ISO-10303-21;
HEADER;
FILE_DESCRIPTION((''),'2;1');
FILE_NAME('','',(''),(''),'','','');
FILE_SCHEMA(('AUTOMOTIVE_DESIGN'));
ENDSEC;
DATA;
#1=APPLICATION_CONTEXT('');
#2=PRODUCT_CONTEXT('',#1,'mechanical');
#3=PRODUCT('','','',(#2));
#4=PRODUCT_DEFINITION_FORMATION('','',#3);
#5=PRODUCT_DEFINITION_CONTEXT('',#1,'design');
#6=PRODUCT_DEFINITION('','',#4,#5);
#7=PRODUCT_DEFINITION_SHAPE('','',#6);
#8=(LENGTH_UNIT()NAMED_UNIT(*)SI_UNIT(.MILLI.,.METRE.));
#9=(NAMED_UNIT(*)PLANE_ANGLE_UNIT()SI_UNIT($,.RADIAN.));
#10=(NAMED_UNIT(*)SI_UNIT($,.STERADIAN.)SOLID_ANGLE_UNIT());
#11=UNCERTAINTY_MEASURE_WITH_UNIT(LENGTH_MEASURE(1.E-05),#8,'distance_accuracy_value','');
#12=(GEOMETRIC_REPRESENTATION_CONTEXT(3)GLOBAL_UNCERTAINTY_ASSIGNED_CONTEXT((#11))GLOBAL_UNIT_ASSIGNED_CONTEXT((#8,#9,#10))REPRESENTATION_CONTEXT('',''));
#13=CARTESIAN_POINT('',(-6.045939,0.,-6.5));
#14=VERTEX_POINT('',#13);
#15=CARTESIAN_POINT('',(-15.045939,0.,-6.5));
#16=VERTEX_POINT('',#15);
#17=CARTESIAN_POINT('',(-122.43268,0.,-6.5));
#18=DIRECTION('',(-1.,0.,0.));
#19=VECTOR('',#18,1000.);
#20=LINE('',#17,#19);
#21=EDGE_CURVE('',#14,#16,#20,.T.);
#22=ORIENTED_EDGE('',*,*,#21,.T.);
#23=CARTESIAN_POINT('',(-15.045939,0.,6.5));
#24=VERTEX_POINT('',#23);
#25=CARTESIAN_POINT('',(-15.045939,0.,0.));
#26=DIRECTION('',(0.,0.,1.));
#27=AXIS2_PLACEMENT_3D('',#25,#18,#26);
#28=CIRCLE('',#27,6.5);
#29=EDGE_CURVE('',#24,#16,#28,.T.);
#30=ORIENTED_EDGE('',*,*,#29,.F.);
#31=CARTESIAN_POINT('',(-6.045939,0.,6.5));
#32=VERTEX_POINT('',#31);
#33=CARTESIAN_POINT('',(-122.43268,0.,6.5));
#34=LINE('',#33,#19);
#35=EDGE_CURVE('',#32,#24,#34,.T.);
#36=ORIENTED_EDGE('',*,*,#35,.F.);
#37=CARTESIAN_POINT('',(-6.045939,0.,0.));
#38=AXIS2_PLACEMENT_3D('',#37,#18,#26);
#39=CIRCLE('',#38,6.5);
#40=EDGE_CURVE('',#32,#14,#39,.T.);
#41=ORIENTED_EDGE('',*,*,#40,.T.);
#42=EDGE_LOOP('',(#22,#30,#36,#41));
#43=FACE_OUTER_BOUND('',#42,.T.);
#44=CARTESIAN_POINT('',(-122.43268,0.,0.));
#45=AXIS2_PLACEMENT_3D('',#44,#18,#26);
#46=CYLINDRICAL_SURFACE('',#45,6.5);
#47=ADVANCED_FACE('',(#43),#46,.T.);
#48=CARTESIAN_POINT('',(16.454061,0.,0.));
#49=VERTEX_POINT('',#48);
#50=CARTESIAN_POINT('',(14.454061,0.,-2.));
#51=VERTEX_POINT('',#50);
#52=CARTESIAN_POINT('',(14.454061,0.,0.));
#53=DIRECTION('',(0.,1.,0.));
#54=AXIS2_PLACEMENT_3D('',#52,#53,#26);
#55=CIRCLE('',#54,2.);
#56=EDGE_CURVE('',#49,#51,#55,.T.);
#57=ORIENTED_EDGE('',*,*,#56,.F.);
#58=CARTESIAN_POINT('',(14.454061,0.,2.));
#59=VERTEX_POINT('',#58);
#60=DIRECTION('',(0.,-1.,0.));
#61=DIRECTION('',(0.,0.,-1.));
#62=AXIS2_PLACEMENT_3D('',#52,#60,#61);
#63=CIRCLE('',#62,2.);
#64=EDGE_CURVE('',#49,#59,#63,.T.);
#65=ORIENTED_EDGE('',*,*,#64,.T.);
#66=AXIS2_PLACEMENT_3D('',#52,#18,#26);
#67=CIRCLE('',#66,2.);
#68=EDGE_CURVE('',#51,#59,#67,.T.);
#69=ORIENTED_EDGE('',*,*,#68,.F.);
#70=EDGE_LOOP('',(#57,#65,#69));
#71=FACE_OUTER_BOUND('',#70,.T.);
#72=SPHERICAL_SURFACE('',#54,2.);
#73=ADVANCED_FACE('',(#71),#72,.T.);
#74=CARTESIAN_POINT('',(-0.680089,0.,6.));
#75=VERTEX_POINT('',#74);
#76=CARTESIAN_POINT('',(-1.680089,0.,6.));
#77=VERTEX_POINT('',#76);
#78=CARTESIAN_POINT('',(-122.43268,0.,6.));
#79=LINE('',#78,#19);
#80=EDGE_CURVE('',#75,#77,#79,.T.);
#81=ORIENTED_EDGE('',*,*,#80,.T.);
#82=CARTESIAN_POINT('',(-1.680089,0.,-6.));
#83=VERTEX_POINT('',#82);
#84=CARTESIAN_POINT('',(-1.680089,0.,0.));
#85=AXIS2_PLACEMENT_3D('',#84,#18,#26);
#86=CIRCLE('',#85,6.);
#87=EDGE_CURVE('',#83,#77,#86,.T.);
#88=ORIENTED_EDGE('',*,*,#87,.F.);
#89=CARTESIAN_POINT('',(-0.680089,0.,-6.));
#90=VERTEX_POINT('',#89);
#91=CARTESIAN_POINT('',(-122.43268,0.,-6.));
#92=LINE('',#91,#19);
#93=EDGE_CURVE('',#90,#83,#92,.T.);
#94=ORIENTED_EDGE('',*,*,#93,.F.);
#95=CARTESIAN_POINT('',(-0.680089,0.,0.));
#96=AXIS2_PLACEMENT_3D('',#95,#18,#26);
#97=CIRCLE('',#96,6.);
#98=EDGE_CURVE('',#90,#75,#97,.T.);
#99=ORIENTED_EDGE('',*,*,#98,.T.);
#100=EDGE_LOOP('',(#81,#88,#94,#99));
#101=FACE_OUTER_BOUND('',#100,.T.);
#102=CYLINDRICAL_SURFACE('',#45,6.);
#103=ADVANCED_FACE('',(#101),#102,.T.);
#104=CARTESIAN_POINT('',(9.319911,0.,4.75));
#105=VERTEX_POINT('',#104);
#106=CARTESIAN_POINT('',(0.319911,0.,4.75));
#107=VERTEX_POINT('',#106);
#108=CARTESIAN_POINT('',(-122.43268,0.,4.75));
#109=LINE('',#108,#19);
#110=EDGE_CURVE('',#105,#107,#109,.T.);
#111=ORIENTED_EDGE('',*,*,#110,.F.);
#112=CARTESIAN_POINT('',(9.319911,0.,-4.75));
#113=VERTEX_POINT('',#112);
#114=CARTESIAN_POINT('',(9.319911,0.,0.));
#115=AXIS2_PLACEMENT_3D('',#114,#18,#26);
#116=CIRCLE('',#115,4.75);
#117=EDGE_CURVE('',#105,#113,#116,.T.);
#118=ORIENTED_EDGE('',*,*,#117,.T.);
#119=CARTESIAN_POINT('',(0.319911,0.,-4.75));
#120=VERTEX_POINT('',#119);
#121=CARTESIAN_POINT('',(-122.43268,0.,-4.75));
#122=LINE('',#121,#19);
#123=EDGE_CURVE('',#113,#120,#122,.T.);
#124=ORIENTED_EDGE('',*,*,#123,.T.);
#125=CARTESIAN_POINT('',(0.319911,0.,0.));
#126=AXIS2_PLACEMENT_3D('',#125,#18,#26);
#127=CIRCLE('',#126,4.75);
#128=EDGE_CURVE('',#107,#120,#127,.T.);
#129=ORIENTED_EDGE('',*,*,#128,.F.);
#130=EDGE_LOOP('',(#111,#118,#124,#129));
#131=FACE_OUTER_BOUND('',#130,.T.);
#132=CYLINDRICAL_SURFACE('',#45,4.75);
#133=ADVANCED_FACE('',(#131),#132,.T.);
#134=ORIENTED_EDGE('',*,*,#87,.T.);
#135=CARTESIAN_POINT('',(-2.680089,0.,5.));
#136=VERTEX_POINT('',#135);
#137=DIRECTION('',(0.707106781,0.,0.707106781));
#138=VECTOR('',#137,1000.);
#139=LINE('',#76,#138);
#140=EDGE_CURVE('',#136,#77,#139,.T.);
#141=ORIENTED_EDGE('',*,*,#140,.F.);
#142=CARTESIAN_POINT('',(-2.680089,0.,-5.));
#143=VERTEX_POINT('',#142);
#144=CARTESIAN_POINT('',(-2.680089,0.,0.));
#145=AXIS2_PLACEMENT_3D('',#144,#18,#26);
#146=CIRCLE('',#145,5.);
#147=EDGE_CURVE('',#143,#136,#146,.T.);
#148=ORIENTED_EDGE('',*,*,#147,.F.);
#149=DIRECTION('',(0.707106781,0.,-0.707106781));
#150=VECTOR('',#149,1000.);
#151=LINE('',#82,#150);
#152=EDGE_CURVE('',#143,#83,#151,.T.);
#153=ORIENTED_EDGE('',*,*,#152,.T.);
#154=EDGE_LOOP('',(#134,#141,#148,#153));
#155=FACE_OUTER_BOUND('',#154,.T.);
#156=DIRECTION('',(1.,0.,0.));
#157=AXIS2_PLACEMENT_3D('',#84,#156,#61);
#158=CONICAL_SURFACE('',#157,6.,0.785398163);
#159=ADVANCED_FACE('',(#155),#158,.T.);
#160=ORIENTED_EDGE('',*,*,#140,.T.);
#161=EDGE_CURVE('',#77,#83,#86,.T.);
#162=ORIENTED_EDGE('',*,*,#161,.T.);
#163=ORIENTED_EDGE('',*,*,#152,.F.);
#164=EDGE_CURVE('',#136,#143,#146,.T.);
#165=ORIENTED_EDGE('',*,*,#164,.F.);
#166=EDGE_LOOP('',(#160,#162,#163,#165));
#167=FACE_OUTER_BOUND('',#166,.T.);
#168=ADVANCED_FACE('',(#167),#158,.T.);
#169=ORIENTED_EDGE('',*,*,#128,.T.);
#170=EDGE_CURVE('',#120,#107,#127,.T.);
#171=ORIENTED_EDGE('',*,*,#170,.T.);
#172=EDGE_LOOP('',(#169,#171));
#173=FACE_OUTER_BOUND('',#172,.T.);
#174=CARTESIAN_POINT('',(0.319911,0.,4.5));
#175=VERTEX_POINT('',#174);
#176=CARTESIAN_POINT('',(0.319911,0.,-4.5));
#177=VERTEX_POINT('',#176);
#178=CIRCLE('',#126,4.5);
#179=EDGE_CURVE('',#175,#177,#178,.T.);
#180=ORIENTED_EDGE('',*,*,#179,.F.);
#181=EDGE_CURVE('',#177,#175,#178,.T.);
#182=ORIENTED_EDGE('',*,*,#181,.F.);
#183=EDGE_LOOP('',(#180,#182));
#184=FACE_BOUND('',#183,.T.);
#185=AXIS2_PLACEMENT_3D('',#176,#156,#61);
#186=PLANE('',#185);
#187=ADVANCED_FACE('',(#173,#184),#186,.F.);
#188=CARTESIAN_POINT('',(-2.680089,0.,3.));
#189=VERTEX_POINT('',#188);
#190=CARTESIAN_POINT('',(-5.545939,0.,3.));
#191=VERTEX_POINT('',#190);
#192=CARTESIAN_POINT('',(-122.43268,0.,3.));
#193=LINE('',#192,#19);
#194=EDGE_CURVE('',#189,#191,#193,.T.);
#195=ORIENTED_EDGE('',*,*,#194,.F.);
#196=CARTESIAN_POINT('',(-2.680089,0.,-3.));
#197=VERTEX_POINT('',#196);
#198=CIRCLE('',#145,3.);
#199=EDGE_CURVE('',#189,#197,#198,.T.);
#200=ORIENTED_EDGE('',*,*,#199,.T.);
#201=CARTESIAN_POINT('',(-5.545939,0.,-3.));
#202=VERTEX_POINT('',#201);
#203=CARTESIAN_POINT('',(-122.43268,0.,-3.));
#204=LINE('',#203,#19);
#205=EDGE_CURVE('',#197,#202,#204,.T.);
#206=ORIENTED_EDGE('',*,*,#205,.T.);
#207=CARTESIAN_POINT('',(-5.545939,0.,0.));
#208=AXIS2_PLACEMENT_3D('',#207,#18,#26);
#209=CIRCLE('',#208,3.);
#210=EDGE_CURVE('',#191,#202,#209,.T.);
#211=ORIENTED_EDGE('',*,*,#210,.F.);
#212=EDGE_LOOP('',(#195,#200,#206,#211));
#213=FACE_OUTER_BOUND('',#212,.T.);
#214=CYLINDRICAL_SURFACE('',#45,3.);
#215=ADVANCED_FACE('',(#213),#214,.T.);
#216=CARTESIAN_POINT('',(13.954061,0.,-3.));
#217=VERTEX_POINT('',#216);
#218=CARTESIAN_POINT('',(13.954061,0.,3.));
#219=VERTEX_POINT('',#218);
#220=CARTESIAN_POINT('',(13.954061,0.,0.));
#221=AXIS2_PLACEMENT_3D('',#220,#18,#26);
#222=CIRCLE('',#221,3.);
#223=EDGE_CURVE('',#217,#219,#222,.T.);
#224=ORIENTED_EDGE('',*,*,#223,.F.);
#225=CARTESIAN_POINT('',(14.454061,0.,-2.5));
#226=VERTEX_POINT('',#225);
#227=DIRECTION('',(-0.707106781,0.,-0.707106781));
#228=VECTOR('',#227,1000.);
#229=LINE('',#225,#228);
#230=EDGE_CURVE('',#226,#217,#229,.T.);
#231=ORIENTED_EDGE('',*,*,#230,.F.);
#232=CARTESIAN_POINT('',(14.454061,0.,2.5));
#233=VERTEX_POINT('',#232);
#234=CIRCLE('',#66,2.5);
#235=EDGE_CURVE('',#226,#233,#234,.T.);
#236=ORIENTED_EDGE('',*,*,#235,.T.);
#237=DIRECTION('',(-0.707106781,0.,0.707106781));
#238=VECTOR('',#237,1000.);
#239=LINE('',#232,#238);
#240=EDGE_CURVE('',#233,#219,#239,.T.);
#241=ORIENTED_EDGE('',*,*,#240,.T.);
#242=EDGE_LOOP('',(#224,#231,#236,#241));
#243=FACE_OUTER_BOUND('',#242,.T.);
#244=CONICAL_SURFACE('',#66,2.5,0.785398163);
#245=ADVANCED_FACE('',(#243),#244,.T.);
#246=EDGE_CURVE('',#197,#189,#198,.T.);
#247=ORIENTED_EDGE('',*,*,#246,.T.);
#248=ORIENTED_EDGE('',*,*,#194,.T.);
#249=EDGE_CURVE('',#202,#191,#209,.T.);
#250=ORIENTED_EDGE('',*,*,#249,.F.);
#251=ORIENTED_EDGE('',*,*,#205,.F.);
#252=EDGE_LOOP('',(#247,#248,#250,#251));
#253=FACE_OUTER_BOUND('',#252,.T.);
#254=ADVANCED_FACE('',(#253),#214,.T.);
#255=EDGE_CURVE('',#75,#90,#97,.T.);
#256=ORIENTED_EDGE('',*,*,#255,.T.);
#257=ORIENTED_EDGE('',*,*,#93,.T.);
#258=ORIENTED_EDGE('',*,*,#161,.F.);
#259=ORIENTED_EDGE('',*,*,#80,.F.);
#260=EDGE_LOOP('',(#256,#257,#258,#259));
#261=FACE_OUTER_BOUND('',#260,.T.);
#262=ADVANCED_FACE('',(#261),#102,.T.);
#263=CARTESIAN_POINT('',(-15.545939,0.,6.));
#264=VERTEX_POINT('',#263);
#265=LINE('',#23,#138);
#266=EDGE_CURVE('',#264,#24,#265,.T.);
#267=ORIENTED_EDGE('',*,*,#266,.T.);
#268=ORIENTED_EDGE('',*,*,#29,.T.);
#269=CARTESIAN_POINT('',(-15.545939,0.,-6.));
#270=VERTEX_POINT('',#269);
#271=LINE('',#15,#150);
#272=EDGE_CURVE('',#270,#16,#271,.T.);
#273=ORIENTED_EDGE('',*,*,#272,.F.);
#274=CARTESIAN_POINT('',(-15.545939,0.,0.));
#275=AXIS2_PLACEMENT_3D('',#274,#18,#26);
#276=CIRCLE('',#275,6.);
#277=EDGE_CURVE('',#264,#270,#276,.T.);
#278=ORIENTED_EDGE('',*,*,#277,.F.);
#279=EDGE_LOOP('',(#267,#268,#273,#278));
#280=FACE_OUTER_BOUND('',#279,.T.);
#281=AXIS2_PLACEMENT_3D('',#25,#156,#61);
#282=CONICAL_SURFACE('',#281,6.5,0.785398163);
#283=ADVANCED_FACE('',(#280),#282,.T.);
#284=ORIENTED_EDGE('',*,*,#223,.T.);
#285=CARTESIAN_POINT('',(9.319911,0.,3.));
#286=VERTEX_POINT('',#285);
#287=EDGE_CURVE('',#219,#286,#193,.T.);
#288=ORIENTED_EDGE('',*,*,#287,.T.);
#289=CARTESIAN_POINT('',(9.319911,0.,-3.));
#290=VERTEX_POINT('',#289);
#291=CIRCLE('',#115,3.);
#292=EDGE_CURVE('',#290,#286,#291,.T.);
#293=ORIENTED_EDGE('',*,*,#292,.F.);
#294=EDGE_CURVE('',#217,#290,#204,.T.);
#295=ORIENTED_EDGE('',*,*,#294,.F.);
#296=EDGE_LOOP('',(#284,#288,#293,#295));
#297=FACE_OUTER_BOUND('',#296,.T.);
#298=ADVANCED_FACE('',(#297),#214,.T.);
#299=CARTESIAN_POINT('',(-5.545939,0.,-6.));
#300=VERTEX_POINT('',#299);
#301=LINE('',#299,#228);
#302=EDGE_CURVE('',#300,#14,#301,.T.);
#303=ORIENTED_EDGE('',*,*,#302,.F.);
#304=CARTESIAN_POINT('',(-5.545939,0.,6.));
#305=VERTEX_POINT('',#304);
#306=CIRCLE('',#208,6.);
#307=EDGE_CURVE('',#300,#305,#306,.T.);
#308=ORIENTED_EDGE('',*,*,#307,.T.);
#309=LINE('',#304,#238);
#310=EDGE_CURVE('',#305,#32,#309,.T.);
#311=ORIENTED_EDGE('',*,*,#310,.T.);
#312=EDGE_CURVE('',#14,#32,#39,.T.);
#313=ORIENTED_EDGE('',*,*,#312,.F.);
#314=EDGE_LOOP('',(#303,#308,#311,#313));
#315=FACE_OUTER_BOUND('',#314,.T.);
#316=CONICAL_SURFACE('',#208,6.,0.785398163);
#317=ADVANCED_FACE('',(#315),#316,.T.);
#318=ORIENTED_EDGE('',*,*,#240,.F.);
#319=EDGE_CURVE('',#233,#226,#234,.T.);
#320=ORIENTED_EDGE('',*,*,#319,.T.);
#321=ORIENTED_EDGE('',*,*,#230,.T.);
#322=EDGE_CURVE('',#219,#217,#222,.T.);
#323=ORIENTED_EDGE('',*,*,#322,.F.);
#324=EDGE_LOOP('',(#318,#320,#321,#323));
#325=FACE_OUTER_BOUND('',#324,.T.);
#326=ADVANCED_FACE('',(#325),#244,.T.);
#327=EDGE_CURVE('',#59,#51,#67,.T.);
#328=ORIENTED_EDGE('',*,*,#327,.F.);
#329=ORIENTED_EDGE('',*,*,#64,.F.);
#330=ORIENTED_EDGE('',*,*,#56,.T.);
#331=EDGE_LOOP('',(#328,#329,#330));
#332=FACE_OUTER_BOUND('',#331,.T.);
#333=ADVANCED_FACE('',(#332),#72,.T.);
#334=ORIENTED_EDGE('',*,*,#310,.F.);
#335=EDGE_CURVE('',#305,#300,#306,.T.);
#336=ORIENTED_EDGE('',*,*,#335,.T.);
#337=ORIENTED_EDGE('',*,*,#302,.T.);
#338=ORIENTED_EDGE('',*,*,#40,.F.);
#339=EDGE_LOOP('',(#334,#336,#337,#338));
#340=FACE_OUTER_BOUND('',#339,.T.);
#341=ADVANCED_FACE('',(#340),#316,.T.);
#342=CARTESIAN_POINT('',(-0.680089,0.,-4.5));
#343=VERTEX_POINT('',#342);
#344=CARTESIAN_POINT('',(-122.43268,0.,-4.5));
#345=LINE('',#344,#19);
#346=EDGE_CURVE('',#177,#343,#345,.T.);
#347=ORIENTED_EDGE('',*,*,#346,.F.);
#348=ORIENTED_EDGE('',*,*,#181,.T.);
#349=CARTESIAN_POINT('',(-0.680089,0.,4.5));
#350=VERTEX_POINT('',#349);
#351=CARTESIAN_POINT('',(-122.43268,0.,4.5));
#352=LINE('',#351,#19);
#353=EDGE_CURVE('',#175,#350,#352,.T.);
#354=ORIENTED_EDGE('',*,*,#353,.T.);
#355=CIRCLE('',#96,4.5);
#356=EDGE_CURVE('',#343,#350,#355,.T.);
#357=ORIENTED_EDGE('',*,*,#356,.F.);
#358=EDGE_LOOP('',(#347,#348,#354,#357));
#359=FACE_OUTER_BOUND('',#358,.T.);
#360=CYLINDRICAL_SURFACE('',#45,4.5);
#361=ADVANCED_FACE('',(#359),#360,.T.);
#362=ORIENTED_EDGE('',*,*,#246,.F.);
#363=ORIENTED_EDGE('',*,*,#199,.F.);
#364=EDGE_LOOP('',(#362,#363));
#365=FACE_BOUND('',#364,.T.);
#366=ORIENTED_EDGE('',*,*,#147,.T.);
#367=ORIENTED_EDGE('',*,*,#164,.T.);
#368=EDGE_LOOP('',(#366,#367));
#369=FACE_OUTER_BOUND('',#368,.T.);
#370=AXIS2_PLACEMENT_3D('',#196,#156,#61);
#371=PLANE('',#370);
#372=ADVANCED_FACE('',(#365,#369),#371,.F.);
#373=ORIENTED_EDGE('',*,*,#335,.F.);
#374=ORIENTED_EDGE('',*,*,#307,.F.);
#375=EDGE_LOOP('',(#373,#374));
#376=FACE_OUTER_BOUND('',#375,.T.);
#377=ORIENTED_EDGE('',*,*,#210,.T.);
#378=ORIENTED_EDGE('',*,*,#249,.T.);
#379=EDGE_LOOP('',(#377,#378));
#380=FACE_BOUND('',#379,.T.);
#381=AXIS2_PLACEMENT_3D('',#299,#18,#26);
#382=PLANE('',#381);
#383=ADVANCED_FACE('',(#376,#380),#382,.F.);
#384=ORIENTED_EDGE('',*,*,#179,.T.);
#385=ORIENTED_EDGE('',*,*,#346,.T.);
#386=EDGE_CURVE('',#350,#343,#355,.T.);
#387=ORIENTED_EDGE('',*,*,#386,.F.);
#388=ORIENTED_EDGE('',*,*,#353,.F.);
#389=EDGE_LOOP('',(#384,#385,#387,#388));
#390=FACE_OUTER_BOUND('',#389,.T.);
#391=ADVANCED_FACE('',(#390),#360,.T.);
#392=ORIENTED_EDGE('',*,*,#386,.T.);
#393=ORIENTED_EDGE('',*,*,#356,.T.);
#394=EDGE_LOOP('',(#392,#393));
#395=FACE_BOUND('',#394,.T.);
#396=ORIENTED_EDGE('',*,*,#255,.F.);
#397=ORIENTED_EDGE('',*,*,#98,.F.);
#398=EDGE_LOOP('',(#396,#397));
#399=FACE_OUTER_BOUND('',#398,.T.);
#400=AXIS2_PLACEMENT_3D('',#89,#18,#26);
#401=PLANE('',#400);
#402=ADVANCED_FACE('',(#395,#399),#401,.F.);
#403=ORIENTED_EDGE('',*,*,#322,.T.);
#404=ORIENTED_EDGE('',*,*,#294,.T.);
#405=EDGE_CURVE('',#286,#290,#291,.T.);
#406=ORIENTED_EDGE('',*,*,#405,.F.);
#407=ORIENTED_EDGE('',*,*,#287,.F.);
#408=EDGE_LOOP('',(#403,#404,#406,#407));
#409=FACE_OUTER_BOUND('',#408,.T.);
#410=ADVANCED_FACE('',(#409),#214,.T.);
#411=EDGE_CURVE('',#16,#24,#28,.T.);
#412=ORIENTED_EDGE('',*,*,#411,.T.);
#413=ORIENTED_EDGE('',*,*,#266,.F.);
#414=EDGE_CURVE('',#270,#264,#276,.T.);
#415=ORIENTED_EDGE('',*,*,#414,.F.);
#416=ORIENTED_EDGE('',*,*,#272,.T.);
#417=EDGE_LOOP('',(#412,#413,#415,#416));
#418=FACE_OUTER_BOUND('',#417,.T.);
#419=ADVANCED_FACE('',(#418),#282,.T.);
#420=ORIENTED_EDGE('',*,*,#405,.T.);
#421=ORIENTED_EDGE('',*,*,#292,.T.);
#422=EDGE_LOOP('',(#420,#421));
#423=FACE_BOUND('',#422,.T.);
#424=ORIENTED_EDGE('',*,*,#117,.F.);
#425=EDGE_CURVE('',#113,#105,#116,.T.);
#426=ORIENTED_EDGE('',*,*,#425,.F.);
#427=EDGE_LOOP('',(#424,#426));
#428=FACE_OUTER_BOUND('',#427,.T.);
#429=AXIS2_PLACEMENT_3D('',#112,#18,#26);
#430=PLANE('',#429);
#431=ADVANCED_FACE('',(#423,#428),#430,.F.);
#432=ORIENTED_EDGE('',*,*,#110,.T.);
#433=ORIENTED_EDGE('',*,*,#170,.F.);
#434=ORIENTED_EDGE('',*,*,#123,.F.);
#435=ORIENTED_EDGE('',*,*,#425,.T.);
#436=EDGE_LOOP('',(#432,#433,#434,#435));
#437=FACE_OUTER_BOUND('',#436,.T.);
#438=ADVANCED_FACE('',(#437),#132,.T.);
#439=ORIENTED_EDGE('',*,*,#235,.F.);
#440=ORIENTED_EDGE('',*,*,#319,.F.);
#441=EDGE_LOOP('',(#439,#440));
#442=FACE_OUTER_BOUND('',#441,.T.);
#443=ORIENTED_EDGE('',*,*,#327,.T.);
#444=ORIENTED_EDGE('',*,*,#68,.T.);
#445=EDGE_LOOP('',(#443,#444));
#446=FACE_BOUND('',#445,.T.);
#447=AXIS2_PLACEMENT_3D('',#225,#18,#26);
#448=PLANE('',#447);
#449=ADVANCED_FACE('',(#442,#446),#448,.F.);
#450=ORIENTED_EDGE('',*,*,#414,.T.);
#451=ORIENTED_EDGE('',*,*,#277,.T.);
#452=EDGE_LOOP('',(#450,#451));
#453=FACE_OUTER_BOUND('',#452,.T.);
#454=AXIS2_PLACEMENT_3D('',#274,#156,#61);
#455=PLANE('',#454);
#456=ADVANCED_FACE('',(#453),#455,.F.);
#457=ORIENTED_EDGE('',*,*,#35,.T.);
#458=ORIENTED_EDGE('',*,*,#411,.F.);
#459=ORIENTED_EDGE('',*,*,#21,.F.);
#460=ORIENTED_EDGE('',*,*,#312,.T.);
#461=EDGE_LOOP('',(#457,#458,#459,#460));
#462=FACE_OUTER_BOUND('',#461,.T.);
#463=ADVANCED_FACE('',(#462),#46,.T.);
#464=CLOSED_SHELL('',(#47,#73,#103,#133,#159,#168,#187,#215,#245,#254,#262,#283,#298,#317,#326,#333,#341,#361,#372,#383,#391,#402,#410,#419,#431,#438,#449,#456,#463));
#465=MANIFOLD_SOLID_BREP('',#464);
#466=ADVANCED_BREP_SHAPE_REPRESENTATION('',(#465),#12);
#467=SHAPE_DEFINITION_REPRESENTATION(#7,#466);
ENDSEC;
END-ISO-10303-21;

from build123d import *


with BuildPart() as part:
    # Sketch1 → Revolve1 (revolve)
    with BuildSketch(Plane(origin=(0, 0, 0), x_dir=(1, 0, 0), z_dir=(0, 1, 0)), mode=Mode.PRIVATE) as revolve1_sk:
        with BuildLine():
            Line((-15.545938878, 0), (-15.545938878, 6))
            Line((-15.545938878, 6), (-15.045938878, 6.5))
            Line((-15.045938878, 6.5), (-6.045938878, 6.5))
            Line((-6.045938878, 6.5), (-5.545938878, 6))
            Line((-5.545938878, 6), (-5.545938878, 3))
            Line((-5.545938878, 3), (-2.680089485, 3))
            Line((-2.680089485, 3), (-2.680089485, 5))
            Line((-2.680089485, 5), (-1.680089485, 6))
            Line((-1.680089485, 6), (-0.680089485, 6))
            Line((-0.680089485, 6), (-0.680089485, 4.5))
            Line((-0.680089485, 4.5), (0.319910515, 4.5))
            Line((0.319910515, 4.5), (0.319910515, 4.75))
            Line((0.319910515, 4.75), (9.319910515, 4.75))
            Line((9.319910515, 4.75), (9.319910515, 3))
            Line((9.319910515, 3), (13.954061122, 3))
            Line((13.954061122, 3), (14.454061122, 2.5))
            Line((14.454061122, 2.5), (14.454061122, 2))
            ThreePointArc((14.454061122, 2), (15.868274684, 1.414213562), (16.454061122, 0))
            Line((16.454061122, 0), (-15.545938878, 0))
        make_face()
    revolve(revolve1_sk.sketch.rotate(Axis((-122.432679922, 0, 0), (1, 0, 0)), 180), axis=Axis((-122.432679922, 0, 0), (1, 0, 0)))


solid = part.part
